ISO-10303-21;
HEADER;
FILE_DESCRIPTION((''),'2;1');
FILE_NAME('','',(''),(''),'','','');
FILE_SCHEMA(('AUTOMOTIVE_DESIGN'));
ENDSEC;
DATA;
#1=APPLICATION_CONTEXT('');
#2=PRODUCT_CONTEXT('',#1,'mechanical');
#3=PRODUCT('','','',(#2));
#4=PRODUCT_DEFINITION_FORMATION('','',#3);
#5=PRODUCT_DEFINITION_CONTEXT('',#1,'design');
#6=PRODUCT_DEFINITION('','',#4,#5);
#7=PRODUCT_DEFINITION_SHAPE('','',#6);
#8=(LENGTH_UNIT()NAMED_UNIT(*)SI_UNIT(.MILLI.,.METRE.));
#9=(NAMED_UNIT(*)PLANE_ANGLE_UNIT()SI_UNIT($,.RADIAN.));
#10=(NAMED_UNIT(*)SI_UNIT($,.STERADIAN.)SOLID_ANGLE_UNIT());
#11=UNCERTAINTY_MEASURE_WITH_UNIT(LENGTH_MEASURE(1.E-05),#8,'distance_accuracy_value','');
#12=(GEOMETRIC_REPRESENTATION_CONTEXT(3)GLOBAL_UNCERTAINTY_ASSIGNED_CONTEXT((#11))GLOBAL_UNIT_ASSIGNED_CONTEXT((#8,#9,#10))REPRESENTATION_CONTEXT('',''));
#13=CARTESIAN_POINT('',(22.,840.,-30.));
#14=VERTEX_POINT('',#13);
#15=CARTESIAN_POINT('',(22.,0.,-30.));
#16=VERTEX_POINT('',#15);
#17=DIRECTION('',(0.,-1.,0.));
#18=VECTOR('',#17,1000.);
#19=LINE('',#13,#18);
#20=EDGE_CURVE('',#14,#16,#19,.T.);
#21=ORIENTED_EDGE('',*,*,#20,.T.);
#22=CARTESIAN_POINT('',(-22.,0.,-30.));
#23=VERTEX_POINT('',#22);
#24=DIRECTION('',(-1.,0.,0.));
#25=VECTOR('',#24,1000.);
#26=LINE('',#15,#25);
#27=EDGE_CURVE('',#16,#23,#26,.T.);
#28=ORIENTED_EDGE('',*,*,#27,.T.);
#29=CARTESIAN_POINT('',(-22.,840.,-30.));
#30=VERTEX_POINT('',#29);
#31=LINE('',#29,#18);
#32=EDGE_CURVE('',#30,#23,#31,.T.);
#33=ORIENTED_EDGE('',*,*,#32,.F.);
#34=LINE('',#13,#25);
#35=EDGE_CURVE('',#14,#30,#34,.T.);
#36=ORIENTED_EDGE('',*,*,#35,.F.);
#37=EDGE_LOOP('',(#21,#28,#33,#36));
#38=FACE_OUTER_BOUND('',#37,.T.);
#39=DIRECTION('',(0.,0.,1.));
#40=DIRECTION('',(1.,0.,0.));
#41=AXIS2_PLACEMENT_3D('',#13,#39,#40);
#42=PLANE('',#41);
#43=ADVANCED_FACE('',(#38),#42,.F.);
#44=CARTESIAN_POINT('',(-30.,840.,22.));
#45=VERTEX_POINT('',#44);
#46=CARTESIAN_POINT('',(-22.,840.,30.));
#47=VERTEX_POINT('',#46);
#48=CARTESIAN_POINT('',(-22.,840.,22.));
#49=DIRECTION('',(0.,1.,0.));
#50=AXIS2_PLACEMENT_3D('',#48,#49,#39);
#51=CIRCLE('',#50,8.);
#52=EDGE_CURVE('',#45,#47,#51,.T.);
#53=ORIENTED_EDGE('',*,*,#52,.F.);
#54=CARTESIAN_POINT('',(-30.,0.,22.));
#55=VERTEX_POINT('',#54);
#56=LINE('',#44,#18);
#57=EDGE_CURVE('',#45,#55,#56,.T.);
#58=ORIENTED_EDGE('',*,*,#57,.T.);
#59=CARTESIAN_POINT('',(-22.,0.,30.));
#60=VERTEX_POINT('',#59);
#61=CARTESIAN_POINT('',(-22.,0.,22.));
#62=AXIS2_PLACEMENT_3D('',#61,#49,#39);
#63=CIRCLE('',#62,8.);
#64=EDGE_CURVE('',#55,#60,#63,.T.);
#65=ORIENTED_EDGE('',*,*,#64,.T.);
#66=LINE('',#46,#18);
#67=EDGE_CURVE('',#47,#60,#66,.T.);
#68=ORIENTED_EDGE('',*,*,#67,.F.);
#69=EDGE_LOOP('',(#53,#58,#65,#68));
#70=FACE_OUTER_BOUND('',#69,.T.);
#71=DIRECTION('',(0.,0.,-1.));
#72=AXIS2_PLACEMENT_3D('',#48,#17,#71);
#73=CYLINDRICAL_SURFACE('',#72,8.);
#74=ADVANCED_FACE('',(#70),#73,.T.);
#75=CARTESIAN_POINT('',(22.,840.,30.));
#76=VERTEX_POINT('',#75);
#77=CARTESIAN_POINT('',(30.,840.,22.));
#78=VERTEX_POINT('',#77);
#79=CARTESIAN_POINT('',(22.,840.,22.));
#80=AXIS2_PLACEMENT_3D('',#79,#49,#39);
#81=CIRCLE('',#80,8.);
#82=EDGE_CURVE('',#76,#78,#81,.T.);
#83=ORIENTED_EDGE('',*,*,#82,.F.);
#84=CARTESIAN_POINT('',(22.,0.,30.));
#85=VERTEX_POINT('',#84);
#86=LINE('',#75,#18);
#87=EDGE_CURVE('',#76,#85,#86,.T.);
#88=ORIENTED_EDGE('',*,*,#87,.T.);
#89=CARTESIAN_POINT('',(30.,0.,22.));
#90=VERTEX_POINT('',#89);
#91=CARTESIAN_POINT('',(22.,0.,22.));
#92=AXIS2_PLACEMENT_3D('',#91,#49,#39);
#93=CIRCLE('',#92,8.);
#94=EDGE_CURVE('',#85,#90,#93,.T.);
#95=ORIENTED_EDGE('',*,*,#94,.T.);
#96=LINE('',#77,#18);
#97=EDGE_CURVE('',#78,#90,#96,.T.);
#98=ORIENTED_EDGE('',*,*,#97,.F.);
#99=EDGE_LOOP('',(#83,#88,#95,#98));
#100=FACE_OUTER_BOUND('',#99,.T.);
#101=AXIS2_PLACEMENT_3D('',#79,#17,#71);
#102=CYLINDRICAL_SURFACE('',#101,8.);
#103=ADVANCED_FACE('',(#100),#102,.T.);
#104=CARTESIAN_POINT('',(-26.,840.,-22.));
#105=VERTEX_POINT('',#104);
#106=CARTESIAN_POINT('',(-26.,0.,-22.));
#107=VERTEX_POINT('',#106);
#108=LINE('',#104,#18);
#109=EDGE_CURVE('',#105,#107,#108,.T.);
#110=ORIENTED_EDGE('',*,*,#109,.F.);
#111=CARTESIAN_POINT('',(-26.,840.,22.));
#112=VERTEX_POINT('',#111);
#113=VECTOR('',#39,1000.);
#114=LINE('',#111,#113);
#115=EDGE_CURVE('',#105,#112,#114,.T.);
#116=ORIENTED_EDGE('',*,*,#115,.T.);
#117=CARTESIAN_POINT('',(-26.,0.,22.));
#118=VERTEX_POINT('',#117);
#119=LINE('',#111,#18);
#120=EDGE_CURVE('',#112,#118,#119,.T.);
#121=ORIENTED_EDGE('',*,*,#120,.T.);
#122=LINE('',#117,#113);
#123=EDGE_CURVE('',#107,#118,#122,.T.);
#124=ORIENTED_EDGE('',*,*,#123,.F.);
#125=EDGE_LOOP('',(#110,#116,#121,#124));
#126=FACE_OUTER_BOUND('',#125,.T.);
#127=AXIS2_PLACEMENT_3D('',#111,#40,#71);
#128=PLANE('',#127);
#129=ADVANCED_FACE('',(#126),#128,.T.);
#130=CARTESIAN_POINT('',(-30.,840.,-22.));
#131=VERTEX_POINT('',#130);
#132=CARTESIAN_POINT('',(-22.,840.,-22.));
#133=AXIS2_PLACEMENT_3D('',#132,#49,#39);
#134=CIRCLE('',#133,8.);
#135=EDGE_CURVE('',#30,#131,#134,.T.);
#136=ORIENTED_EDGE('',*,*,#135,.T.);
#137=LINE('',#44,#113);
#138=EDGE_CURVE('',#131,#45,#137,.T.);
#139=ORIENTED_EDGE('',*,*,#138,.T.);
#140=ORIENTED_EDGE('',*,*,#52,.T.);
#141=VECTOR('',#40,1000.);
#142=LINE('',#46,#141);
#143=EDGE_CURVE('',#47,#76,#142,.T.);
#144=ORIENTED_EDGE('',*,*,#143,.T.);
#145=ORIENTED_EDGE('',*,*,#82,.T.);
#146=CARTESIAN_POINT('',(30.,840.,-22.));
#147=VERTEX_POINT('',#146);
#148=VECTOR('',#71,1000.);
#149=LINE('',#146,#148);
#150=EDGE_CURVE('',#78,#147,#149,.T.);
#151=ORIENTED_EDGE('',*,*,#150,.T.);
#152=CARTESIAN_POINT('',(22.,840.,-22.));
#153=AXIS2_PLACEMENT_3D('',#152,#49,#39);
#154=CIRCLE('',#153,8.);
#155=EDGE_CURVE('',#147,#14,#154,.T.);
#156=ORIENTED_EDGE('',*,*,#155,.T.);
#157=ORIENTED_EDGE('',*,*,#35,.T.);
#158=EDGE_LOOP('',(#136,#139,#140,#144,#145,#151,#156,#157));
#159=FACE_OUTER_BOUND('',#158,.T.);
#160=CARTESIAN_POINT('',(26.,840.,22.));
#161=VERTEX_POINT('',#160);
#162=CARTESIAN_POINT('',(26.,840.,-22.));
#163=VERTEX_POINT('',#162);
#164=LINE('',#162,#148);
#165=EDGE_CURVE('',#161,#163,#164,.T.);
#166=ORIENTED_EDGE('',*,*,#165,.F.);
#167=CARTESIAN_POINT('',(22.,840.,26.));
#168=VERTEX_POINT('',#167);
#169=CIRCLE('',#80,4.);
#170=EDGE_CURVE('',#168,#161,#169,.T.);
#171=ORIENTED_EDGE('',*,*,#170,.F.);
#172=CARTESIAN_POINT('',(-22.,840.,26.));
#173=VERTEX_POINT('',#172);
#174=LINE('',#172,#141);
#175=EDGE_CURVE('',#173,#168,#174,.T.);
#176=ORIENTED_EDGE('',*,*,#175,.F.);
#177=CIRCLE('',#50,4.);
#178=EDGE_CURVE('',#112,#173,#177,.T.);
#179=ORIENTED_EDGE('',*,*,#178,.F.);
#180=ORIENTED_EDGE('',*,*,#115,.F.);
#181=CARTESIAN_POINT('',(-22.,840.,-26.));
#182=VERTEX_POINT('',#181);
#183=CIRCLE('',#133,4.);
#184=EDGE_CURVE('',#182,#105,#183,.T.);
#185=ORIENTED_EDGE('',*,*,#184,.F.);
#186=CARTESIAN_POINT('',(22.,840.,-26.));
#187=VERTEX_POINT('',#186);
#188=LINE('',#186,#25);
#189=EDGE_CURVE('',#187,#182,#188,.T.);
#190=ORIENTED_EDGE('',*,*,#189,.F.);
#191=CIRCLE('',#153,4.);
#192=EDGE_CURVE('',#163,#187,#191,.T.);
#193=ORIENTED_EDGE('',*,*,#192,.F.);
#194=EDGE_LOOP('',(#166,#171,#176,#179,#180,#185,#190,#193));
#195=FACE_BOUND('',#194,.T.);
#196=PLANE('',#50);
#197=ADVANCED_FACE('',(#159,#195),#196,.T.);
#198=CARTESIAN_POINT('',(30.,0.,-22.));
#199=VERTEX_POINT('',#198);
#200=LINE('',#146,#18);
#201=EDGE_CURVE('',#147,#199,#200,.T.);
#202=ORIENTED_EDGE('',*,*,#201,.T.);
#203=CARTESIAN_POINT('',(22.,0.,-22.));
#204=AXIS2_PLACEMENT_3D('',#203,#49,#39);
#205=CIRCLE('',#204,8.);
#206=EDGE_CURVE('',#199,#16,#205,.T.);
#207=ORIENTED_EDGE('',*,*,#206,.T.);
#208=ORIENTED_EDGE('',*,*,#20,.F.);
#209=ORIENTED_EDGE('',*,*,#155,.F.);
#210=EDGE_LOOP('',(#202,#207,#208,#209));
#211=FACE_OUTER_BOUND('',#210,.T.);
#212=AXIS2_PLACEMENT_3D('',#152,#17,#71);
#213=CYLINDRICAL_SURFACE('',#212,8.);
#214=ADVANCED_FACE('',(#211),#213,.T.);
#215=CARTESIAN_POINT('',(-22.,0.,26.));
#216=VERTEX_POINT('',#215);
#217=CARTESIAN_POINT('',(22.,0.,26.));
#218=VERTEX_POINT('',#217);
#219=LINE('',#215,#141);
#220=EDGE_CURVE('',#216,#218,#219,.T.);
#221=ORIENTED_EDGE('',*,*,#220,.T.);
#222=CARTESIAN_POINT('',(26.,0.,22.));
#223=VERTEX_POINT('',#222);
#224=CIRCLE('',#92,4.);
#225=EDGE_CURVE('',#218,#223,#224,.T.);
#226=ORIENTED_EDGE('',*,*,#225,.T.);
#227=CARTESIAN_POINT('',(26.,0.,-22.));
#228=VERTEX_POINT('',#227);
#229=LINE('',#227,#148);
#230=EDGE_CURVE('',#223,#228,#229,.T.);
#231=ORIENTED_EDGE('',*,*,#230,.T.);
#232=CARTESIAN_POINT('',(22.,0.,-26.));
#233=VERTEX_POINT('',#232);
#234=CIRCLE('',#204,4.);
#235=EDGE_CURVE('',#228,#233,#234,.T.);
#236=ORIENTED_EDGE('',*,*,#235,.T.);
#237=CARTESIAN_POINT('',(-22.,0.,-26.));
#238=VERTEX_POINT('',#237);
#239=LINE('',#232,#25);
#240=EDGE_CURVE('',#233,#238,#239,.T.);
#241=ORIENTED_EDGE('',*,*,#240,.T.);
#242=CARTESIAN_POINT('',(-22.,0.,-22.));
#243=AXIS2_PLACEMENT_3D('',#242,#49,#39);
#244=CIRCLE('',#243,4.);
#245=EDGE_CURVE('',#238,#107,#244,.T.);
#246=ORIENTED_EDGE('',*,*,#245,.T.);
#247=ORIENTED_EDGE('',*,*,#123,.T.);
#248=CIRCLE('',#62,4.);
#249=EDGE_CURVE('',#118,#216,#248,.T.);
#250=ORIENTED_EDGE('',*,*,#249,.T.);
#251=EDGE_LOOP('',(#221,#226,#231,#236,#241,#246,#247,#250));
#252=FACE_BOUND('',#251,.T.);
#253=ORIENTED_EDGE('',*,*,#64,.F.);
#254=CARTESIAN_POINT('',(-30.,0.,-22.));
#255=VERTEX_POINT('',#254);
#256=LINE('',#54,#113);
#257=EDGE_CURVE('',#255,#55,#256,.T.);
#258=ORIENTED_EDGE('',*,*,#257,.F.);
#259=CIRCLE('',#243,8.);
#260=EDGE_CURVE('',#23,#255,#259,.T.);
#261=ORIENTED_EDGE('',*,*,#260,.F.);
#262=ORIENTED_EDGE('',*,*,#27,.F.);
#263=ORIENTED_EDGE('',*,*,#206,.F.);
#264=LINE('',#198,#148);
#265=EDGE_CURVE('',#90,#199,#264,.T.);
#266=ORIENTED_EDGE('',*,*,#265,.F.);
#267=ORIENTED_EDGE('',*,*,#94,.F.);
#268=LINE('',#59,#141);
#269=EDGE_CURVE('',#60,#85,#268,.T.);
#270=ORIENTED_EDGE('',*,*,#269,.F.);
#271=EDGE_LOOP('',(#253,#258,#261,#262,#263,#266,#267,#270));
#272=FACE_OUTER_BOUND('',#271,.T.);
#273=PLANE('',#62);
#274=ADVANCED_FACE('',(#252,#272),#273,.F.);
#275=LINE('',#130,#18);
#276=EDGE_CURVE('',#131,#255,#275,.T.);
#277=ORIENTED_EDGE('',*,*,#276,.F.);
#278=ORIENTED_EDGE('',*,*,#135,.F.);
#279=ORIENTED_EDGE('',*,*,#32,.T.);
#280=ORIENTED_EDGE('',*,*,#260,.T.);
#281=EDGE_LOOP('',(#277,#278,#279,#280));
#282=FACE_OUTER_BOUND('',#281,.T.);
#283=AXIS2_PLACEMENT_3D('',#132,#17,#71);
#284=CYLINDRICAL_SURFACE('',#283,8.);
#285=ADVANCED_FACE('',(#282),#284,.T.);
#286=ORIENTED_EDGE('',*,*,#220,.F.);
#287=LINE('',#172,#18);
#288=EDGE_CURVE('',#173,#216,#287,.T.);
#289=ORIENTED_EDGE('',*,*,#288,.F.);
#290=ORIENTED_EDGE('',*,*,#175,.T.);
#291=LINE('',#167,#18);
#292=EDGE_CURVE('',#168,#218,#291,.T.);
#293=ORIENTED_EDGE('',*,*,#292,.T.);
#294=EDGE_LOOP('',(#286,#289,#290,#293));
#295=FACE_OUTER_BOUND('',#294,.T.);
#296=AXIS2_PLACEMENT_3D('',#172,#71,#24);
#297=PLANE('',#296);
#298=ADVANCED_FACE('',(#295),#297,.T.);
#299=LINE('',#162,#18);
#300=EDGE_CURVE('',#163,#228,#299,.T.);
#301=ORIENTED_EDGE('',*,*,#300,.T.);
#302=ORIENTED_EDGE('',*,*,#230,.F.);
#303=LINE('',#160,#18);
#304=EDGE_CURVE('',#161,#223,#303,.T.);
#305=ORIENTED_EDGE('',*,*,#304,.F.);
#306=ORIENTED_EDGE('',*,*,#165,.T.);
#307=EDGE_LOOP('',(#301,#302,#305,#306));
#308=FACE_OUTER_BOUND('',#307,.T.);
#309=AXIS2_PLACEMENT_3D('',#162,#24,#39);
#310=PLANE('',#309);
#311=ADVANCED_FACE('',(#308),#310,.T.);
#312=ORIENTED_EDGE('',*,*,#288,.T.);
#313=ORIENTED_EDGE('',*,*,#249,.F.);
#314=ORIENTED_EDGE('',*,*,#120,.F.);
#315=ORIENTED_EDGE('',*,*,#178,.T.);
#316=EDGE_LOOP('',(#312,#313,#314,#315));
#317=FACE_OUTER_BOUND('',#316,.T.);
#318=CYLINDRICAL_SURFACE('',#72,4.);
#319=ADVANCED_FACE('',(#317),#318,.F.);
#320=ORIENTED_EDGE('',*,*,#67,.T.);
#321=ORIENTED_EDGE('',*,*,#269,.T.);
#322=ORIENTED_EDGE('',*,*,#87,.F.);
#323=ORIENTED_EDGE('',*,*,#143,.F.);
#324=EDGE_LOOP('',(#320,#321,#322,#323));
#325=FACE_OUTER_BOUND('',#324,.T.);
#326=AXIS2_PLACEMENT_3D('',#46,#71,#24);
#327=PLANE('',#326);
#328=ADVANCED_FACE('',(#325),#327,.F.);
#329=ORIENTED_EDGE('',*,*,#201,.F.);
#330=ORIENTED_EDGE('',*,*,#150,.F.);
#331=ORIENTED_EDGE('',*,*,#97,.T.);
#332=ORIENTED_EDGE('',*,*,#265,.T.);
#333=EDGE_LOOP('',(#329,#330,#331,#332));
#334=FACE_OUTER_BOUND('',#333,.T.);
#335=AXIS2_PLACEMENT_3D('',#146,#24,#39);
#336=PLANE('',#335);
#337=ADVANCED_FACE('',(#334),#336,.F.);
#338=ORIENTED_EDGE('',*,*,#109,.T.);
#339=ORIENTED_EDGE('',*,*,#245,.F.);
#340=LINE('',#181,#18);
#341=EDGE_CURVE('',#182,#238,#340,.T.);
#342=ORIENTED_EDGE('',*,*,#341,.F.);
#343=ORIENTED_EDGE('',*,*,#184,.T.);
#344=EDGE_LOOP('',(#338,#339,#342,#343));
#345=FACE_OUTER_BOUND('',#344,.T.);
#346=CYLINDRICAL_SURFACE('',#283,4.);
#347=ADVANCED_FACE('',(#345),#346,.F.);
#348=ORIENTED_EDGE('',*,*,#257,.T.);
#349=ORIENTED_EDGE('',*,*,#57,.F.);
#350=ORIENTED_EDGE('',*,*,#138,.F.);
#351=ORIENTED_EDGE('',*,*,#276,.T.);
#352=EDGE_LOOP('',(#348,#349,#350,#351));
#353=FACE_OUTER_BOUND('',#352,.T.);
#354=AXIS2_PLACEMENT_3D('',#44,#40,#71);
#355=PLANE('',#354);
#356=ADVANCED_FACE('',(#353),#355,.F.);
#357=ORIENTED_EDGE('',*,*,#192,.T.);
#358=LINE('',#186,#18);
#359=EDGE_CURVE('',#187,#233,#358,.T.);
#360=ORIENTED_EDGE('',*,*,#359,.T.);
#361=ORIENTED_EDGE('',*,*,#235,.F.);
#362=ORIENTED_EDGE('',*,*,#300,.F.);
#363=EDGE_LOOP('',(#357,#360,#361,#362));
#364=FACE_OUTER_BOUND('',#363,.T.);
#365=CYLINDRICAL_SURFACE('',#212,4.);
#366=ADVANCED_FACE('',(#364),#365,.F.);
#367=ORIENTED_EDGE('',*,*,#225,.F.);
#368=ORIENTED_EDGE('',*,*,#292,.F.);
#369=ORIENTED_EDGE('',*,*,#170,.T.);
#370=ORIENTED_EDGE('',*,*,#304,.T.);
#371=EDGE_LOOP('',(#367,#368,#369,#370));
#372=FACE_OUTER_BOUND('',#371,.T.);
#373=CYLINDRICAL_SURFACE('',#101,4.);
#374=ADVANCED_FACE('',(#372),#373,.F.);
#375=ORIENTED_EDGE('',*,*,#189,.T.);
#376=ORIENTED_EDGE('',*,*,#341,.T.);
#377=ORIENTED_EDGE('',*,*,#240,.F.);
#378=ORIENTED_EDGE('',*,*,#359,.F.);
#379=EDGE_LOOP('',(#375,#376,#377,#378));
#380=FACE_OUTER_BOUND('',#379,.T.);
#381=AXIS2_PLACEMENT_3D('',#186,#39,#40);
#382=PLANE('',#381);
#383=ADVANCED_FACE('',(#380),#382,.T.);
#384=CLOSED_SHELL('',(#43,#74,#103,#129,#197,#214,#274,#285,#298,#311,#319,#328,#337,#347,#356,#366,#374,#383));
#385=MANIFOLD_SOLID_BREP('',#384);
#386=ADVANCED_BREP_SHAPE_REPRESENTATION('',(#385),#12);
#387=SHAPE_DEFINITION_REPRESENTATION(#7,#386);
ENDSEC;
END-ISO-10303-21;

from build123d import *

# Parameters (mm, degrees)
GB_T_6728_2002_SQUARE_HOLLOW_SECTION_60_DEPTH = 840


with BuildPart() as part:
    # Sketch1 → GB/T 6728-2002 square hollow section 60×60×4(1) (new body)
    with BuildSketch(Plane(origin=(0, 0, 0), x_dir=(-1, 0, 0), z_dir=(0, 1, 0))):
        with BuildLine():
            Line((-22, -30), (22, -30))
            ThreePointArc((22, -30), (27.656854249, -27.656854249), (30, -22))
            Line((30, -22), (30, 22))
            ThreePointArc((30, 22), (27.656854249, 27.656854249), (22, 30))
            Line((22, 30), (-22, 30))
            ThreePointArc((-22, 30), (-27.656854249, 27.656854249), (-30, 22))
            Line((-30, 22), (-30, -22))
            ThreePointArc((-30, -22), (-27.656854249, -27.656854249), (-22, -30))
        make_face()
        with BuildLine():
            Line((-22, -26), (22, -26))
            ThreePointArc((22, -26), (24.828427125, -24.828427125), (26, -22))
            Line((26, -22), (26, 22))
            ThreePointArc((26, 22), (24.828427125, 24.828427125), (22, 26))
            Line((22, 26), (-22, 26))
            ThreePointArc((-22, 26), (-24.828427125, 24.828427125), (-26, 22))
            Line((-26, 22), (-26, -22))
            ThreePointArc((-26, -22), (-24.828427125, -24.828427125), (-22, -26))
        make_face(mode=Mode.SUBTRACT)
    extrude(amount=GB_T_6728_2002_SQUARE_HOLLOW_SECTION_60_DEPTH)


solid = part.part
